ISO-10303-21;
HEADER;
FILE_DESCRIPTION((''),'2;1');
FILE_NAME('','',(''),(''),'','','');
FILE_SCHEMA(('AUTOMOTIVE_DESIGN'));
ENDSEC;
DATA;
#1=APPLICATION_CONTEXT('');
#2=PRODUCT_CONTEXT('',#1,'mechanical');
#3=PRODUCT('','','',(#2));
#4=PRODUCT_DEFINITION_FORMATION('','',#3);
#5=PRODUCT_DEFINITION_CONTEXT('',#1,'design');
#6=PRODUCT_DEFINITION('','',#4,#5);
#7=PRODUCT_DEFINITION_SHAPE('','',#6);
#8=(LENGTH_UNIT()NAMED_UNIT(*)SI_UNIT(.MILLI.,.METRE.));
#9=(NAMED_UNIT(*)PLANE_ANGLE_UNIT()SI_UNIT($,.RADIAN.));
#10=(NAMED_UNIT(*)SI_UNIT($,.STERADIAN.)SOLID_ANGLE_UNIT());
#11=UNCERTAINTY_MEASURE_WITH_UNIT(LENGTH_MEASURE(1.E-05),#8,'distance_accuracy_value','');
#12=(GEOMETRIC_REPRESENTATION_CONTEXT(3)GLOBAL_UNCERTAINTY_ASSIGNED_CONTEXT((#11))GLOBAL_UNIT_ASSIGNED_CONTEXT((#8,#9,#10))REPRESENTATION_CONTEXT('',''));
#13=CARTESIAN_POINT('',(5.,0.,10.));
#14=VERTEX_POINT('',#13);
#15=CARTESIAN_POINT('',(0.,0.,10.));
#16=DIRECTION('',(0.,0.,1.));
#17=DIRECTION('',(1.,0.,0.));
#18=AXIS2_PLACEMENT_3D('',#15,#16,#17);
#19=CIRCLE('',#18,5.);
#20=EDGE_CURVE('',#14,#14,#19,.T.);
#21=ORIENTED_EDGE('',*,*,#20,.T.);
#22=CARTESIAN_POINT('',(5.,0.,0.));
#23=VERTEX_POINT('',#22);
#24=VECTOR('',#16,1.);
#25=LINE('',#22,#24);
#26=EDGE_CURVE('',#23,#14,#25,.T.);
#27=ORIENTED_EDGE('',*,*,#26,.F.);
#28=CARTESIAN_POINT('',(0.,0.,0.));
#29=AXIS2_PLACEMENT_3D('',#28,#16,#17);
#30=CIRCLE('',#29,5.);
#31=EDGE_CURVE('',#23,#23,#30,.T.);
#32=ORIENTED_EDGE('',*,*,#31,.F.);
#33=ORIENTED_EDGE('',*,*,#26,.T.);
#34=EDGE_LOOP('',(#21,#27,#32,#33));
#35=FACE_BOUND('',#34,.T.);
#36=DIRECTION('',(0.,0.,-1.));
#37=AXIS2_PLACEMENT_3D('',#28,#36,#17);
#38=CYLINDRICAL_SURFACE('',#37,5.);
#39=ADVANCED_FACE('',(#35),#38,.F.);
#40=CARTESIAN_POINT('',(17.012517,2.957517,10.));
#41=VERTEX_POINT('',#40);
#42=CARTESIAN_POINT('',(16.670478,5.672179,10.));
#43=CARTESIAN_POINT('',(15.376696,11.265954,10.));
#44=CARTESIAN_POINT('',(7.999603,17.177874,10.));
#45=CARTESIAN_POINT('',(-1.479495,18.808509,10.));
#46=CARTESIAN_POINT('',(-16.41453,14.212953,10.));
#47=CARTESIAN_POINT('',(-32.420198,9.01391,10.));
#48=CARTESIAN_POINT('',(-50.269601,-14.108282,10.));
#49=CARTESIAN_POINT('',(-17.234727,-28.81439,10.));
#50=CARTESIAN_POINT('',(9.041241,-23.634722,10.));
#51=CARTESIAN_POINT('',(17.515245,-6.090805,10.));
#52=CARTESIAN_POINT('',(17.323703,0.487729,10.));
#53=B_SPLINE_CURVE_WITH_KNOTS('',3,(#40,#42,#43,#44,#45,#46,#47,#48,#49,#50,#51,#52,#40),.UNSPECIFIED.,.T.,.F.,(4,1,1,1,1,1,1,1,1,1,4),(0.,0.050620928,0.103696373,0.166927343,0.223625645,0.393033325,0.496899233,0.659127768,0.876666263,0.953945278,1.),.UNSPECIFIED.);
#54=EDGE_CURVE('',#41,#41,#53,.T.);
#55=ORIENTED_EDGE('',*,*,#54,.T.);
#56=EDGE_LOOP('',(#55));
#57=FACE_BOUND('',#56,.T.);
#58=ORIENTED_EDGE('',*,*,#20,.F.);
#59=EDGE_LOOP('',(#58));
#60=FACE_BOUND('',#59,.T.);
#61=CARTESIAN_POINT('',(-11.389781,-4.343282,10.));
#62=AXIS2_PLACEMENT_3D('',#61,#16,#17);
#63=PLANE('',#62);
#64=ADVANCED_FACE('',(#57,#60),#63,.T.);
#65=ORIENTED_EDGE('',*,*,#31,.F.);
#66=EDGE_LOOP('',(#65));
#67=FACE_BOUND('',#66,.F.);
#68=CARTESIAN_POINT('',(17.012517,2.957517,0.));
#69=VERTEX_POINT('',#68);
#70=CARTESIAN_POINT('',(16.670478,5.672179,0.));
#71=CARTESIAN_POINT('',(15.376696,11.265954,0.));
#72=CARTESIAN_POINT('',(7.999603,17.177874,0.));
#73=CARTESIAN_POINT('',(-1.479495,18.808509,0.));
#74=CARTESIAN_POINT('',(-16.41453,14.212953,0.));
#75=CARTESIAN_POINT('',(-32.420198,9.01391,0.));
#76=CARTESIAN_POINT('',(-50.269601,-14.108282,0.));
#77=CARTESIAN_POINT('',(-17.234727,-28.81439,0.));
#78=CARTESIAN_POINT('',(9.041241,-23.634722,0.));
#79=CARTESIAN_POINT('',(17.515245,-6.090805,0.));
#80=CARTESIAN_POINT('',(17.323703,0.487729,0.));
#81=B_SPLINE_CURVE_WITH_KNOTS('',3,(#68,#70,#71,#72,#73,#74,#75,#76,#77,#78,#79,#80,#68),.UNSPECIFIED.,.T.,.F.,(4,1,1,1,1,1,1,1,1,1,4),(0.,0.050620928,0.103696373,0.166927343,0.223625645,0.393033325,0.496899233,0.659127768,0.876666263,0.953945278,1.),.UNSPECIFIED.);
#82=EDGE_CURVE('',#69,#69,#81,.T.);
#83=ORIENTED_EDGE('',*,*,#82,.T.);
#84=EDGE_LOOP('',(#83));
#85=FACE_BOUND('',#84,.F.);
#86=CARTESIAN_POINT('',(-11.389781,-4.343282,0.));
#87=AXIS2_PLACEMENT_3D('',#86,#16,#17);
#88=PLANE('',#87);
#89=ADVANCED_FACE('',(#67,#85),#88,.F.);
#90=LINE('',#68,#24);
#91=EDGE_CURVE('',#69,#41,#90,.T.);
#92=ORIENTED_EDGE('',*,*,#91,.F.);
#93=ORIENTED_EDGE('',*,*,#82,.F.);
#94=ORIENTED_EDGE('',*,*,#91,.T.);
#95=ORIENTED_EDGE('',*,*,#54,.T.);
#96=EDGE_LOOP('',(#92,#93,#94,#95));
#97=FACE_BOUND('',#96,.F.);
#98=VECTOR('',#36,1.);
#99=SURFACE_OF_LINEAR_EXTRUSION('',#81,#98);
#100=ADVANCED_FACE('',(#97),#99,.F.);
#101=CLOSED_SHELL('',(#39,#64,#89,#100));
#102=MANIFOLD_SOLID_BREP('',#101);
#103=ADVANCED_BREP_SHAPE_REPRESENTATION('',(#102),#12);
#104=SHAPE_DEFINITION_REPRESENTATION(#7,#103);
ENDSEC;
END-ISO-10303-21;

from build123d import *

# Parameters (mm, degrees)
SKETCH1_R           = 5
BOSS_EXTRUDE1_DEPTH = 10


with BuildPart() as part:
    # Sketch1 → Boss-Extrude1 (new body)
    with BuildSketch(Plane.XY):
        with BuildLine():
            add(Edge.make_bspline(
                [(17.012517442, 2.957517207), (16.670478453, 5.672178927), (15.376695719, 11.265953823), (7.999602539, 17.177874454), (-1.479494805, 18.808508667), (-16.414530478, 14.212952947), (-32.420198414, 9.013909894), (-50.269600748, -14.108282025), (-17.23472676, -28.814390043), (9.041241393, -23.634721545), (17.515245457, -6.090805118), (17.323703177, 0.487728599), (17.012517442, 2.957517207)],
                knots=[0, 0, 0, 0, 0.050620928, 0.103696373, 0.166927343, 0.223625645, 0.393033325, 0.496899233, 0.659127768, 0.876666263, 0.953945278, 1, 1, 1, 1], degree=3))
        make_face()
        Circle(SKETCH1_R, mode=Mode.SUBTRACT)
    extrude(amount=BOSS_EXTRUDE1_DEPTH)


solid = part.part
